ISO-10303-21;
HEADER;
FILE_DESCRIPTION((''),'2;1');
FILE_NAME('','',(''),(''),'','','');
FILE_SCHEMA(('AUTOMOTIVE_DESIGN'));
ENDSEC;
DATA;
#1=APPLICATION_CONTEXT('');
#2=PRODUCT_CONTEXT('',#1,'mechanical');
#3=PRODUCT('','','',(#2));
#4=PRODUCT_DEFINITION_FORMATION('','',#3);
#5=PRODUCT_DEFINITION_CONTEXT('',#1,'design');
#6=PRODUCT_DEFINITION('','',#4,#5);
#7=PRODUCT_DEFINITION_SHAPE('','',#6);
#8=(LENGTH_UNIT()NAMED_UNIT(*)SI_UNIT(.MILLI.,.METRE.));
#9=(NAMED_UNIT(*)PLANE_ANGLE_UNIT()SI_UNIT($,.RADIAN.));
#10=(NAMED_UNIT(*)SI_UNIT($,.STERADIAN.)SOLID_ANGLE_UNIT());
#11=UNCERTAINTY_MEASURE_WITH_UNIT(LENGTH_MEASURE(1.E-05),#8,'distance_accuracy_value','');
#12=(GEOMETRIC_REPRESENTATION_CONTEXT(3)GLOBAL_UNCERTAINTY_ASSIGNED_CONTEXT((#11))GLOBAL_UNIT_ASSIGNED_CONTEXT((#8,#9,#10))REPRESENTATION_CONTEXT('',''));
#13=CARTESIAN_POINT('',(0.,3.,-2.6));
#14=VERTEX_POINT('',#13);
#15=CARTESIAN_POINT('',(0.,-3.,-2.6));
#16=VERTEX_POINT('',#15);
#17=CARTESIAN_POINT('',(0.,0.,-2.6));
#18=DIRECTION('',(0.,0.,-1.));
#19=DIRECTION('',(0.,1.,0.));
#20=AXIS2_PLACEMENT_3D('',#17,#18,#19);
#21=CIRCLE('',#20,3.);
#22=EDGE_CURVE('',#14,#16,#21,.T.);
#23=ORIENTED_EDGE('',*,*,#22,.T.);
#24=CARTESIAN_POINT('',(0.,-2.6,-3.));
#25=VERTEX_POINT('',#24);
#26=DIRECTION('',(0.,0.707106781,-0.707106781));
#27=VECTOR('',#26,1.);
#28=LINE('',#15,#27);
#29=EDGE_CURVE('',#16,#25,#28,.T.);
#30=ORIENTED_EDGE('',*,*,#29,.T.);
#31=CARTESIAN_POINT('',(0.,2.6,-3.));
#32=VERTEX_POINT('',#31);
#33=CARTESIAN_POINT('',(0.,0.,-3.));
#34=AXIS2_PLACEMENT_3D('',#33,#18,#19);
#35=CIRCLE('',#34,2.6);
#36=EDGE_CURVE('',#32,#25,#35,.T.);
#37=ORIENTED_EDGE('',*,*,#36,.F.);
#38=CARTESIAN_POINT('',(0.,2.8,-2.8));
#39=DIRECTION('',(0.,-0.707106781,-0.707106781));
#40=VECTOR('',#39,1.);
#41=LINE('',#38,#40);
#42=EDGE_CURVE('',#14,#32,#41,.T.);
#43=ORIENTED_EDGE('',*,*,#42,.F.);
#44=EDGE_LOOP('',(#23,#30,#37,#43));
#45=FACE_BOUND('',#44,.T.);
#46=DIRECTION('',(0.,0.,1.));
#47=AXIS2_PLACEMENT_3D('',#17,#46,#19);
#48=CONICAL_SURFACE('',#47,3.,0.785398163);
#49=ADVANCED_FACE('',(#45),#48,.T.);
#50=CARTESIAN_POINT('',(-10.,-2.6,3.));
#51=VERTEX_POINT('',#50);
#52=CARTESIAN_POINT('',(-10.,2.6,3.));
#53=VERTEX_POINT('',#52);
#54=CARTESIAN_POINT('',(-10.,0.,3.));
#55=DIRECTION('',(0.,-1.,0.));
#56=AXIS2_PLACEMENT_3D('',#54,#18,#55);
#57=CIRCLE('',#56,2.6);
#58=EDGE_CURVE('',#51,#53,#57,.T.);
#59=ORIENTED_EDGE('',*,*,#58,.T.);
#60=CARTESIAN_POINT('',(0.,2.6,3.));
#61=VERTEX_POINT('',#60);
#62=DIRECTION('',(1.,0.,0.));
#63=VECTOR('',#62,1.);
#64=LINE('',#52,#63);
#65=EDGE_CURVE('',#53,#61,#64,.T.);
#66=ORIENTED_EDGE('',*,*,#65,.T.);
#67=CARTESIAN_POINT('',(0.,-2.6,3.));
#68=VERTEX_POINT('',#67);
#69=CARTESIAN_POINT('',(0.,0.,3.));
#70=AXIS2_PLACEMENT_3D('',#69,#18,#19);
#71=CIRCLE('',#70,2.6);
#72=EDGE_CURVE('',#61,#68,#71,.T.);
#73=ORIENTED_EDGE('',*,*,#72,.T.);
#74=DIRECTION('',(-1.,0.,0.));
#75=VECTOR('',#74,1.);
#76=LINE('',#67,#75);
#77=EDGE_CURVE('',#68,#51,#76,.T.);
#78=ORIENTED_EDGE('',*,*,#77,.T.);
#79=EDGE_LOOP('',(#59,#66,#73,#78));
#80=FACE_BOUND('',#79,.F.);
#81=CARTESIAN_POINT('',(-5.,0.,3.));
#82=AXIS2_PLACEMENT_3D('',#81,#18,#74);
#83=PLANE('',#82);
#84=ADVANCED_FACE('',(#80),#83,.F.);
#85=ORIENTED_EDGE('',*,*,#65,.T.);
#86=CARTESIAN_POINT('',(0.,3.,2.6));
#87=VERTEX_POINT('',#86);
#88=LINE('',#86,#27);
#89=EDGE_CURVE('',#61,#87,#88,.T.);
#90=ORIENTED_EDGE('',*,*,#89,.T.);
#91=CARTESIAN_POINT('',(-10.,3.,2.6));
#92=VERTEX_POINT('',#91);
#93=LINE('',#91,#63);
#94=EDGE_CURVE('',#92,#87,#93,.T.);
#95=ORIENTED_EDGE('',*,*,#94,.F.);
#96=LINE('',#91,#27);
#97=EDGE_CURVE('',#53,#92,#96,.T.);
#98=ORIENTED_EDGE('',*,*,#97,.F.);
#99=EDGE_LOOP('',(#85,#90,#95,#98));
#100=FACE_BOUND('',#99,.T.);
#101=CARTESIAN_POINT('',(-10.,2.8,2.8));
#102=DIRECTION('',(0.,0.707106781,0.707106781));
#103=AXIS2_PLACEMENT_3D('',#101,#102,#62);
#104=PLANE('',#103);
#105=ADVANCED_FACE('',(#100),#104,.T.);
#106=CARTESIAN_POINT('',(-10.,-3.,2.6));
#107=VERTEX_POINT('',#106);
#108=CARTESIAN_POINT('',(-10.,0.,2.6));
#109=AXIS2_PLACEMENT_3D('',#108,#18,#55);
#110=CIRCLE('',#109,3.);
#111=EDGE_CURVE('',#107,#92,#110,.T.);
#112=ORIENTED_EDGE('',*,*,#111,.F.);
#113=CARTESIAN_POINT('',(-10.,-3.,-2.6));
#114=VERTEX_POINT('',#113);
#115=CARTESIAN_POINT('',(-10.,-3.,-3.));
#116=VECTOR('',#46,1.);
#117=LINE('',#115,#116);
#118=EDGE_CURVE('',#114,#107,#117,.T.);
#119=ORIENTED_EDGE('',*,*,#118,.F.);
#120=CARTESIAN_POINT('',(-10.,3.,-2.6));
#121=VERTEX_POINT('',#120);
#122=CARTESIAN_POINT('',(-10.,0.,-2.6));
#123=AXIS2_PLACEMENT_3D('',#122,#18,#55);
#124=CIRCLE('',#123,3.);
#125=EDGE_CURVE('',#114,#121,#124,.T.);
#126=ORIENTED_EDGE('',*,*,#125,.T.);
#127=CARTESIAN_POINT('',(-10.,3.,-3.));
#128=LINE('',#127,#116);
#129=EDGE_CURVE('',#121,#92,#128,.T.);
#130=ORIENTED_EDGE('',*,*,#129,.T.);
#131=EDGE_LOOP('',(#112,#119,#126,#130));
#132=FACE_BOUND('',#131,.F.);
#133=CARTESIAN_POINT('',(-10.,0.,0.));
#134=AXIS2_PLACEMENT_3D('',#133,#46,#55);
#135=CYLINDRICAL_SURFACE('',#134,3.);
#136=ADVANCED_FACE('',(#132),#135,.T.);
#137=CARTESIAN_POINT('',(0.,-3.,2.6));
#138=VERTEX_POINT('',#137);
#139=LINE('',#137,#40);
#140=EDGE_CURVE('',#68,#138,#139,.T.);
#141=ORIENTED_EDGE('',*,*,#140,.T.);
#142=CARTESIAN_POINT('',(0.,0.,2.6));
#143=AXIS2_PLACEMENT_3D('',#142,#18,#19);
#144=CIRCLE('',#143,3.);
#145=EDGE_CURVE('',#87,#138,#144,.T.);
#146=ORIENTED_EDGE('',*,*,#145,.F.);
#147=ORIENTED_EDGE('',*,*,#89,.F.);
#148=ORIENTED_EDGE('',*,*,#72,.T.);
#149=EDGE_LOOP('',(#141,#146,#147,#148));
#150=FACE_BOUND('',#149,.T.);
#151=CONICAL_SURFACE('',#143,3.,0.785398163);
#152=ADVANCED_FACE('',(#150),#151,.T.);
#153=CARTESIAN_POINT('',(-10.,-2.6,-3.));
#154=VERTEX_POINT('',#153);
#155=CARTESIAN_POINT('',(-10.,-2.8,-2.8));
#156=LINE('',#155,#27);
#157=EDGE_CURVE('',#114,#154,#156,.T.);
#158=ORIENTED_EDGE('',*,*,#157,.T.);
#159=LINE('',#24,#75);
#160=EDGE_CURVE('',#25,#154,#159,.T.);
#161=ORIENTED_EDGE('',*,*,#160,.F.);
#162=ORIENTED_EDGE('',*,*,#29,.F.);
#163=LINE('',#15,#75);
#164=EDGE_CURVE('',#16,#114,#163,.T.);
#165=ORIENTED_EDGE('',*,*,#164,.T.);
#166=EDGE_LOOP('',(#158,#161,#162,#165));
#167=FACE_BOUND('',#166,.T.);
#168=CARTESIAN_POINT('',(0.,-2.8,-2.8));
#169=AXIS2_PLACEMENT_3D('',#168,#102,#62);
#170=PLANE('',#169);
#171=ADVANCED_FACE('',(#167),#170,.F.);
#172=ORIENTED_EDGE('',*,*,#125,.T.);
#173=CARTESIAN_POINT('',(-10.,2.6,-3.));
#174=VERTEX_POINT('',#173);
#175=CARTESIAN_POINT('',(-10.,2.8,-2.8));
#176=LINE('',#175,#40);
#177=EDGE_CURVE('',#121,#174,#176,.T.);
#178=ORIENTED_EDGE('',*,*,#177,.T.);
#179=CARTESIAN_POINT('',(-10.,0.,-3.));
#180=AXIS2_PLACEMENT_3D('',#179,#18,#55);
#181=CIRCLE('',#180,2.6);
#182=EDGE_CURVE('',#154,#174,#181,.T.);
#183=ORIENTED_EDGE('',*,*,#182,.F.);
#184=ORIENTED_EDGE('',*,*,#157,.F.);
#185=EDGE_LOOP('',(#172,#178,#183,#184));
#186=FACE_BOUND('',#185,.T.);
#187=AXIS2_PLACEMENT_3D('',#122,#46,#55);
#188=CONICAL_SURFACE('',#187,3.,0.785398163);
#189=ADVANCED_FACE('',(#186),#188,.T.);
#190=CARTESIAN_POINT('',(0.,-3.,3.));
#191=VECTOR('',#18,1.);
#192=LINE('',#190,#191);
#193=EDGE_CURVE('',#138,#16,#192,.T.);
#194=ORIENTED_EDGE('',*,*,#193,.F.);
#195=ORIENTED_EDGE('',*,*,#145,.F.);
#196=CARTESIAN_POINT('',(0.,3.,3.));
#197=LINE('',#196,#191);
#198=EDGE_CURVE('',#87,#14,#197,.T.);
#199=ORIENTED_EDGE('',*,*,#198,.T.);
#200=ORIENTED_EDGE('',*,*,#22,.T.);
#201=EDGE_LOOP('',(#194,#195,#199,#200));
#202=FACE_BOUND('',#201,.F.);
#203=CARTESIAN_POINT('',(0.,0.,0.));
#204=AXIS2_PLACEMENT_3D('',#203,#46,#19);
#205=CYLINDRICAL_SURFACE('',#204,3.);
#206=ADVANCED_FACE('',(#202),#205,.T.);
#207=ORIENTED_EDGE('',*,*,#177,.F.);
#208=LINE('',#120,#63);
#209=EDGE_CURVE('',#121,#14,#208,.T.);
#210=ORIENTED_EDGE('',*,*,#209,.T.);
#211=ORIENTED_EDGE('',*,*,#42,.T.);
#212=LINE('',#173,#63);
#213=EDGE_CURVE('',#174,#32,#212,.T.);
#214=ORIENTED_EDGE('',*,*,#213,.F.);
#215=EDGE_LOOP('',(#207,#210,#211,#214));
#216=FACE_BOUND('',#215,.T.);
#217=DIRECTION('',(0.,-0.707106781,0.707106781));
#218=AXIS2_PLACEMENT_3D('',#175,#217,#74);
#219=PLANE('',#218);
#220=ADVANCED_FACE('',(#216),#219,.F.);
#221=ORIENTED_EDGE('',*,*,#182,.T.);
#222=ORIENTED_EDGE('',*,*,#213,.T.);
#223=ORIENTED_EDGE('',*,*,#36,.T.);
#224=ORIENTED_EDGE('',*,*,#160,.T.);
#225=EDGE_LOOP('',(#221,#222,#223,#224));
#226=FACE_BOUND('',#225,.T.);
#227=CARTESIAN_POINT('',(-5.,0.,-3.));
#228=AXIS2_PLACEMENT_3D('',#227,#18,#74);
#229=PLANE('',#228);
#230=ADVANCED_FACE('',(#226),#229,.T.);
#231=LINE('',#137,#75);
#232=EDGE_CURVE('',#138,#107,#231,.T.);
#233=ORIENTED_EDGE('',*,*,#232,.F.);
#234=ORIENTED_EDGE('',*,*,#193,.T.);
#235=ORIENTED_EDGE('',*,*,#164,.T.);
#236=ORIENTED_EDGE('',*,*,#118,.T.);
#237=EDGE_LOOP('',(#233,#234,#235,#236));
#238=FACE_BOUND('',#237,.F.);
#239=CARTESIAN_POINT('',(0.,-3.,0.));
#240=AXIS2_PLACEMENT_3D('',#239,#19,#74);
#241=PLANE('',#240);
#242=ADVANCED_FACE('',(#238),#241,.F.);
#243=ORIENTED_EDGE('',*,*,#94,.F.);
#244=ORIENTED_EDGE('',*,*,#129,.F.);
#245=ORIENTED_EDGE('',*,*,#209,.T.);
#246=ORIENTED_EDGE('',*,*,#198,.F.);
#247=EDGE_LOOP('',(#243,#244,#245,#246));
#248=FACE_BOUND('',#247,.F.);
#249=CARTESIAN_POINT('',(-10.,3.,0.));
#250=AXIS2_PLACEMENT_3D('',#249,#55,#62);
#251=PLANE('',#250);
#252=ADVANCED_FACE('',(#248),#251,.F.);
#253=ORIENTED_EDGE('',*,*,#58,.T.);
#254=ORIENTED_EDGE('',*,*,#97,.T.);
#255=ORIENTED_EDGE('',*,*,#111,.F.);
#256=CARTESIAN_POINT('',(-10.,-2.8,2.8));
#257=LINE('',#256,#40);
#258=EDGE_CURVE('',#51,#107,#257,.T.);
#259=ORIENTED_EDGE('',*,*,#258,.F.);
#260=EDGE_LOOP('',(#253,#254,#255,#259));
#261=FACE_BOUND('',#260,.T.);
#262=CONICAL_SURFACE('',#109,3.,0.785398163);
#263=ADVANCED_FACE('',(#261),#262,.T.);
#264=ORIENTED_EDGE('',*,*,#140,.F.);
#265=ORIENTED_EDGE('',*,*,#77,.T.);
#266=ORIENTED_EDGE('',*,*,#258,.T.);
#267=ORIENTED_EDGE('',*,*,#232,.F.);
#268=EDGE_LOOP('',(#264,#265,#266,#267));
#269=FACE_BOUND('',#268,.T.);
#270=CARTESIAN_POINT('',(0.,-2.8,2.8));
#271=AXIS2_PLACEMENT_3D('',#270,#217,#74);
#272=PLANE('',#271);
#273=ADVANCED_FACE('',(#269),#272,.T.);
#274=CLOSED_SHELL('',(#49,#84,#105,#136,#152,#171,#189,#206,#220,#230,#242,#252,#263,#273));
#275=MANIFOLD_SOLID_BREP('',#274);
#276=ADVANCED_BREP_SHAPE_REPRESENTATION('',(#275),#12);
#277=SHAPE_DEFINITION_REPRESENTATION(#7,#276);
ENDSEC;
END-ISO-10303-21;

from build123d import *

# Parameters (mm, degrees)
BASEKEY_DEPTH = 3
CHAMFER1_SIZE = 0.4


with BuildPart() as part:
    # Sketch1 → BaseKey (new, symmetric)
    with BuildSketch(Plane.XY):
        with BuildLine():
            Line((-10, 3), (0, 3))
            ThreePointArc((0, 3), (3, 0), (0, -3))
            Line((0, -3), (-10, -3))
            ThreePointArc((-10, -3), (-13, 0), (-10, 3))
        make_face()
    extrude(amount=BASEKEY_DEPTH, both=True)

    # Chamfer1
    chamfer1_edges = [part.edges().sort_by_distance(p)[0] for p in [
        (3, 0, 3),
        (-5, 3, 3),
        (-13, 0, 3),
        (-5, 3, -3),
        (3, 0, -3),
        (-5, -3, -3),
        (-13, 0, -3),
        (-5, -3, 3),
    ]]
    chamfer(chamfer1_edges, length=CHAMFER1_SIZE)


solid = part.part
